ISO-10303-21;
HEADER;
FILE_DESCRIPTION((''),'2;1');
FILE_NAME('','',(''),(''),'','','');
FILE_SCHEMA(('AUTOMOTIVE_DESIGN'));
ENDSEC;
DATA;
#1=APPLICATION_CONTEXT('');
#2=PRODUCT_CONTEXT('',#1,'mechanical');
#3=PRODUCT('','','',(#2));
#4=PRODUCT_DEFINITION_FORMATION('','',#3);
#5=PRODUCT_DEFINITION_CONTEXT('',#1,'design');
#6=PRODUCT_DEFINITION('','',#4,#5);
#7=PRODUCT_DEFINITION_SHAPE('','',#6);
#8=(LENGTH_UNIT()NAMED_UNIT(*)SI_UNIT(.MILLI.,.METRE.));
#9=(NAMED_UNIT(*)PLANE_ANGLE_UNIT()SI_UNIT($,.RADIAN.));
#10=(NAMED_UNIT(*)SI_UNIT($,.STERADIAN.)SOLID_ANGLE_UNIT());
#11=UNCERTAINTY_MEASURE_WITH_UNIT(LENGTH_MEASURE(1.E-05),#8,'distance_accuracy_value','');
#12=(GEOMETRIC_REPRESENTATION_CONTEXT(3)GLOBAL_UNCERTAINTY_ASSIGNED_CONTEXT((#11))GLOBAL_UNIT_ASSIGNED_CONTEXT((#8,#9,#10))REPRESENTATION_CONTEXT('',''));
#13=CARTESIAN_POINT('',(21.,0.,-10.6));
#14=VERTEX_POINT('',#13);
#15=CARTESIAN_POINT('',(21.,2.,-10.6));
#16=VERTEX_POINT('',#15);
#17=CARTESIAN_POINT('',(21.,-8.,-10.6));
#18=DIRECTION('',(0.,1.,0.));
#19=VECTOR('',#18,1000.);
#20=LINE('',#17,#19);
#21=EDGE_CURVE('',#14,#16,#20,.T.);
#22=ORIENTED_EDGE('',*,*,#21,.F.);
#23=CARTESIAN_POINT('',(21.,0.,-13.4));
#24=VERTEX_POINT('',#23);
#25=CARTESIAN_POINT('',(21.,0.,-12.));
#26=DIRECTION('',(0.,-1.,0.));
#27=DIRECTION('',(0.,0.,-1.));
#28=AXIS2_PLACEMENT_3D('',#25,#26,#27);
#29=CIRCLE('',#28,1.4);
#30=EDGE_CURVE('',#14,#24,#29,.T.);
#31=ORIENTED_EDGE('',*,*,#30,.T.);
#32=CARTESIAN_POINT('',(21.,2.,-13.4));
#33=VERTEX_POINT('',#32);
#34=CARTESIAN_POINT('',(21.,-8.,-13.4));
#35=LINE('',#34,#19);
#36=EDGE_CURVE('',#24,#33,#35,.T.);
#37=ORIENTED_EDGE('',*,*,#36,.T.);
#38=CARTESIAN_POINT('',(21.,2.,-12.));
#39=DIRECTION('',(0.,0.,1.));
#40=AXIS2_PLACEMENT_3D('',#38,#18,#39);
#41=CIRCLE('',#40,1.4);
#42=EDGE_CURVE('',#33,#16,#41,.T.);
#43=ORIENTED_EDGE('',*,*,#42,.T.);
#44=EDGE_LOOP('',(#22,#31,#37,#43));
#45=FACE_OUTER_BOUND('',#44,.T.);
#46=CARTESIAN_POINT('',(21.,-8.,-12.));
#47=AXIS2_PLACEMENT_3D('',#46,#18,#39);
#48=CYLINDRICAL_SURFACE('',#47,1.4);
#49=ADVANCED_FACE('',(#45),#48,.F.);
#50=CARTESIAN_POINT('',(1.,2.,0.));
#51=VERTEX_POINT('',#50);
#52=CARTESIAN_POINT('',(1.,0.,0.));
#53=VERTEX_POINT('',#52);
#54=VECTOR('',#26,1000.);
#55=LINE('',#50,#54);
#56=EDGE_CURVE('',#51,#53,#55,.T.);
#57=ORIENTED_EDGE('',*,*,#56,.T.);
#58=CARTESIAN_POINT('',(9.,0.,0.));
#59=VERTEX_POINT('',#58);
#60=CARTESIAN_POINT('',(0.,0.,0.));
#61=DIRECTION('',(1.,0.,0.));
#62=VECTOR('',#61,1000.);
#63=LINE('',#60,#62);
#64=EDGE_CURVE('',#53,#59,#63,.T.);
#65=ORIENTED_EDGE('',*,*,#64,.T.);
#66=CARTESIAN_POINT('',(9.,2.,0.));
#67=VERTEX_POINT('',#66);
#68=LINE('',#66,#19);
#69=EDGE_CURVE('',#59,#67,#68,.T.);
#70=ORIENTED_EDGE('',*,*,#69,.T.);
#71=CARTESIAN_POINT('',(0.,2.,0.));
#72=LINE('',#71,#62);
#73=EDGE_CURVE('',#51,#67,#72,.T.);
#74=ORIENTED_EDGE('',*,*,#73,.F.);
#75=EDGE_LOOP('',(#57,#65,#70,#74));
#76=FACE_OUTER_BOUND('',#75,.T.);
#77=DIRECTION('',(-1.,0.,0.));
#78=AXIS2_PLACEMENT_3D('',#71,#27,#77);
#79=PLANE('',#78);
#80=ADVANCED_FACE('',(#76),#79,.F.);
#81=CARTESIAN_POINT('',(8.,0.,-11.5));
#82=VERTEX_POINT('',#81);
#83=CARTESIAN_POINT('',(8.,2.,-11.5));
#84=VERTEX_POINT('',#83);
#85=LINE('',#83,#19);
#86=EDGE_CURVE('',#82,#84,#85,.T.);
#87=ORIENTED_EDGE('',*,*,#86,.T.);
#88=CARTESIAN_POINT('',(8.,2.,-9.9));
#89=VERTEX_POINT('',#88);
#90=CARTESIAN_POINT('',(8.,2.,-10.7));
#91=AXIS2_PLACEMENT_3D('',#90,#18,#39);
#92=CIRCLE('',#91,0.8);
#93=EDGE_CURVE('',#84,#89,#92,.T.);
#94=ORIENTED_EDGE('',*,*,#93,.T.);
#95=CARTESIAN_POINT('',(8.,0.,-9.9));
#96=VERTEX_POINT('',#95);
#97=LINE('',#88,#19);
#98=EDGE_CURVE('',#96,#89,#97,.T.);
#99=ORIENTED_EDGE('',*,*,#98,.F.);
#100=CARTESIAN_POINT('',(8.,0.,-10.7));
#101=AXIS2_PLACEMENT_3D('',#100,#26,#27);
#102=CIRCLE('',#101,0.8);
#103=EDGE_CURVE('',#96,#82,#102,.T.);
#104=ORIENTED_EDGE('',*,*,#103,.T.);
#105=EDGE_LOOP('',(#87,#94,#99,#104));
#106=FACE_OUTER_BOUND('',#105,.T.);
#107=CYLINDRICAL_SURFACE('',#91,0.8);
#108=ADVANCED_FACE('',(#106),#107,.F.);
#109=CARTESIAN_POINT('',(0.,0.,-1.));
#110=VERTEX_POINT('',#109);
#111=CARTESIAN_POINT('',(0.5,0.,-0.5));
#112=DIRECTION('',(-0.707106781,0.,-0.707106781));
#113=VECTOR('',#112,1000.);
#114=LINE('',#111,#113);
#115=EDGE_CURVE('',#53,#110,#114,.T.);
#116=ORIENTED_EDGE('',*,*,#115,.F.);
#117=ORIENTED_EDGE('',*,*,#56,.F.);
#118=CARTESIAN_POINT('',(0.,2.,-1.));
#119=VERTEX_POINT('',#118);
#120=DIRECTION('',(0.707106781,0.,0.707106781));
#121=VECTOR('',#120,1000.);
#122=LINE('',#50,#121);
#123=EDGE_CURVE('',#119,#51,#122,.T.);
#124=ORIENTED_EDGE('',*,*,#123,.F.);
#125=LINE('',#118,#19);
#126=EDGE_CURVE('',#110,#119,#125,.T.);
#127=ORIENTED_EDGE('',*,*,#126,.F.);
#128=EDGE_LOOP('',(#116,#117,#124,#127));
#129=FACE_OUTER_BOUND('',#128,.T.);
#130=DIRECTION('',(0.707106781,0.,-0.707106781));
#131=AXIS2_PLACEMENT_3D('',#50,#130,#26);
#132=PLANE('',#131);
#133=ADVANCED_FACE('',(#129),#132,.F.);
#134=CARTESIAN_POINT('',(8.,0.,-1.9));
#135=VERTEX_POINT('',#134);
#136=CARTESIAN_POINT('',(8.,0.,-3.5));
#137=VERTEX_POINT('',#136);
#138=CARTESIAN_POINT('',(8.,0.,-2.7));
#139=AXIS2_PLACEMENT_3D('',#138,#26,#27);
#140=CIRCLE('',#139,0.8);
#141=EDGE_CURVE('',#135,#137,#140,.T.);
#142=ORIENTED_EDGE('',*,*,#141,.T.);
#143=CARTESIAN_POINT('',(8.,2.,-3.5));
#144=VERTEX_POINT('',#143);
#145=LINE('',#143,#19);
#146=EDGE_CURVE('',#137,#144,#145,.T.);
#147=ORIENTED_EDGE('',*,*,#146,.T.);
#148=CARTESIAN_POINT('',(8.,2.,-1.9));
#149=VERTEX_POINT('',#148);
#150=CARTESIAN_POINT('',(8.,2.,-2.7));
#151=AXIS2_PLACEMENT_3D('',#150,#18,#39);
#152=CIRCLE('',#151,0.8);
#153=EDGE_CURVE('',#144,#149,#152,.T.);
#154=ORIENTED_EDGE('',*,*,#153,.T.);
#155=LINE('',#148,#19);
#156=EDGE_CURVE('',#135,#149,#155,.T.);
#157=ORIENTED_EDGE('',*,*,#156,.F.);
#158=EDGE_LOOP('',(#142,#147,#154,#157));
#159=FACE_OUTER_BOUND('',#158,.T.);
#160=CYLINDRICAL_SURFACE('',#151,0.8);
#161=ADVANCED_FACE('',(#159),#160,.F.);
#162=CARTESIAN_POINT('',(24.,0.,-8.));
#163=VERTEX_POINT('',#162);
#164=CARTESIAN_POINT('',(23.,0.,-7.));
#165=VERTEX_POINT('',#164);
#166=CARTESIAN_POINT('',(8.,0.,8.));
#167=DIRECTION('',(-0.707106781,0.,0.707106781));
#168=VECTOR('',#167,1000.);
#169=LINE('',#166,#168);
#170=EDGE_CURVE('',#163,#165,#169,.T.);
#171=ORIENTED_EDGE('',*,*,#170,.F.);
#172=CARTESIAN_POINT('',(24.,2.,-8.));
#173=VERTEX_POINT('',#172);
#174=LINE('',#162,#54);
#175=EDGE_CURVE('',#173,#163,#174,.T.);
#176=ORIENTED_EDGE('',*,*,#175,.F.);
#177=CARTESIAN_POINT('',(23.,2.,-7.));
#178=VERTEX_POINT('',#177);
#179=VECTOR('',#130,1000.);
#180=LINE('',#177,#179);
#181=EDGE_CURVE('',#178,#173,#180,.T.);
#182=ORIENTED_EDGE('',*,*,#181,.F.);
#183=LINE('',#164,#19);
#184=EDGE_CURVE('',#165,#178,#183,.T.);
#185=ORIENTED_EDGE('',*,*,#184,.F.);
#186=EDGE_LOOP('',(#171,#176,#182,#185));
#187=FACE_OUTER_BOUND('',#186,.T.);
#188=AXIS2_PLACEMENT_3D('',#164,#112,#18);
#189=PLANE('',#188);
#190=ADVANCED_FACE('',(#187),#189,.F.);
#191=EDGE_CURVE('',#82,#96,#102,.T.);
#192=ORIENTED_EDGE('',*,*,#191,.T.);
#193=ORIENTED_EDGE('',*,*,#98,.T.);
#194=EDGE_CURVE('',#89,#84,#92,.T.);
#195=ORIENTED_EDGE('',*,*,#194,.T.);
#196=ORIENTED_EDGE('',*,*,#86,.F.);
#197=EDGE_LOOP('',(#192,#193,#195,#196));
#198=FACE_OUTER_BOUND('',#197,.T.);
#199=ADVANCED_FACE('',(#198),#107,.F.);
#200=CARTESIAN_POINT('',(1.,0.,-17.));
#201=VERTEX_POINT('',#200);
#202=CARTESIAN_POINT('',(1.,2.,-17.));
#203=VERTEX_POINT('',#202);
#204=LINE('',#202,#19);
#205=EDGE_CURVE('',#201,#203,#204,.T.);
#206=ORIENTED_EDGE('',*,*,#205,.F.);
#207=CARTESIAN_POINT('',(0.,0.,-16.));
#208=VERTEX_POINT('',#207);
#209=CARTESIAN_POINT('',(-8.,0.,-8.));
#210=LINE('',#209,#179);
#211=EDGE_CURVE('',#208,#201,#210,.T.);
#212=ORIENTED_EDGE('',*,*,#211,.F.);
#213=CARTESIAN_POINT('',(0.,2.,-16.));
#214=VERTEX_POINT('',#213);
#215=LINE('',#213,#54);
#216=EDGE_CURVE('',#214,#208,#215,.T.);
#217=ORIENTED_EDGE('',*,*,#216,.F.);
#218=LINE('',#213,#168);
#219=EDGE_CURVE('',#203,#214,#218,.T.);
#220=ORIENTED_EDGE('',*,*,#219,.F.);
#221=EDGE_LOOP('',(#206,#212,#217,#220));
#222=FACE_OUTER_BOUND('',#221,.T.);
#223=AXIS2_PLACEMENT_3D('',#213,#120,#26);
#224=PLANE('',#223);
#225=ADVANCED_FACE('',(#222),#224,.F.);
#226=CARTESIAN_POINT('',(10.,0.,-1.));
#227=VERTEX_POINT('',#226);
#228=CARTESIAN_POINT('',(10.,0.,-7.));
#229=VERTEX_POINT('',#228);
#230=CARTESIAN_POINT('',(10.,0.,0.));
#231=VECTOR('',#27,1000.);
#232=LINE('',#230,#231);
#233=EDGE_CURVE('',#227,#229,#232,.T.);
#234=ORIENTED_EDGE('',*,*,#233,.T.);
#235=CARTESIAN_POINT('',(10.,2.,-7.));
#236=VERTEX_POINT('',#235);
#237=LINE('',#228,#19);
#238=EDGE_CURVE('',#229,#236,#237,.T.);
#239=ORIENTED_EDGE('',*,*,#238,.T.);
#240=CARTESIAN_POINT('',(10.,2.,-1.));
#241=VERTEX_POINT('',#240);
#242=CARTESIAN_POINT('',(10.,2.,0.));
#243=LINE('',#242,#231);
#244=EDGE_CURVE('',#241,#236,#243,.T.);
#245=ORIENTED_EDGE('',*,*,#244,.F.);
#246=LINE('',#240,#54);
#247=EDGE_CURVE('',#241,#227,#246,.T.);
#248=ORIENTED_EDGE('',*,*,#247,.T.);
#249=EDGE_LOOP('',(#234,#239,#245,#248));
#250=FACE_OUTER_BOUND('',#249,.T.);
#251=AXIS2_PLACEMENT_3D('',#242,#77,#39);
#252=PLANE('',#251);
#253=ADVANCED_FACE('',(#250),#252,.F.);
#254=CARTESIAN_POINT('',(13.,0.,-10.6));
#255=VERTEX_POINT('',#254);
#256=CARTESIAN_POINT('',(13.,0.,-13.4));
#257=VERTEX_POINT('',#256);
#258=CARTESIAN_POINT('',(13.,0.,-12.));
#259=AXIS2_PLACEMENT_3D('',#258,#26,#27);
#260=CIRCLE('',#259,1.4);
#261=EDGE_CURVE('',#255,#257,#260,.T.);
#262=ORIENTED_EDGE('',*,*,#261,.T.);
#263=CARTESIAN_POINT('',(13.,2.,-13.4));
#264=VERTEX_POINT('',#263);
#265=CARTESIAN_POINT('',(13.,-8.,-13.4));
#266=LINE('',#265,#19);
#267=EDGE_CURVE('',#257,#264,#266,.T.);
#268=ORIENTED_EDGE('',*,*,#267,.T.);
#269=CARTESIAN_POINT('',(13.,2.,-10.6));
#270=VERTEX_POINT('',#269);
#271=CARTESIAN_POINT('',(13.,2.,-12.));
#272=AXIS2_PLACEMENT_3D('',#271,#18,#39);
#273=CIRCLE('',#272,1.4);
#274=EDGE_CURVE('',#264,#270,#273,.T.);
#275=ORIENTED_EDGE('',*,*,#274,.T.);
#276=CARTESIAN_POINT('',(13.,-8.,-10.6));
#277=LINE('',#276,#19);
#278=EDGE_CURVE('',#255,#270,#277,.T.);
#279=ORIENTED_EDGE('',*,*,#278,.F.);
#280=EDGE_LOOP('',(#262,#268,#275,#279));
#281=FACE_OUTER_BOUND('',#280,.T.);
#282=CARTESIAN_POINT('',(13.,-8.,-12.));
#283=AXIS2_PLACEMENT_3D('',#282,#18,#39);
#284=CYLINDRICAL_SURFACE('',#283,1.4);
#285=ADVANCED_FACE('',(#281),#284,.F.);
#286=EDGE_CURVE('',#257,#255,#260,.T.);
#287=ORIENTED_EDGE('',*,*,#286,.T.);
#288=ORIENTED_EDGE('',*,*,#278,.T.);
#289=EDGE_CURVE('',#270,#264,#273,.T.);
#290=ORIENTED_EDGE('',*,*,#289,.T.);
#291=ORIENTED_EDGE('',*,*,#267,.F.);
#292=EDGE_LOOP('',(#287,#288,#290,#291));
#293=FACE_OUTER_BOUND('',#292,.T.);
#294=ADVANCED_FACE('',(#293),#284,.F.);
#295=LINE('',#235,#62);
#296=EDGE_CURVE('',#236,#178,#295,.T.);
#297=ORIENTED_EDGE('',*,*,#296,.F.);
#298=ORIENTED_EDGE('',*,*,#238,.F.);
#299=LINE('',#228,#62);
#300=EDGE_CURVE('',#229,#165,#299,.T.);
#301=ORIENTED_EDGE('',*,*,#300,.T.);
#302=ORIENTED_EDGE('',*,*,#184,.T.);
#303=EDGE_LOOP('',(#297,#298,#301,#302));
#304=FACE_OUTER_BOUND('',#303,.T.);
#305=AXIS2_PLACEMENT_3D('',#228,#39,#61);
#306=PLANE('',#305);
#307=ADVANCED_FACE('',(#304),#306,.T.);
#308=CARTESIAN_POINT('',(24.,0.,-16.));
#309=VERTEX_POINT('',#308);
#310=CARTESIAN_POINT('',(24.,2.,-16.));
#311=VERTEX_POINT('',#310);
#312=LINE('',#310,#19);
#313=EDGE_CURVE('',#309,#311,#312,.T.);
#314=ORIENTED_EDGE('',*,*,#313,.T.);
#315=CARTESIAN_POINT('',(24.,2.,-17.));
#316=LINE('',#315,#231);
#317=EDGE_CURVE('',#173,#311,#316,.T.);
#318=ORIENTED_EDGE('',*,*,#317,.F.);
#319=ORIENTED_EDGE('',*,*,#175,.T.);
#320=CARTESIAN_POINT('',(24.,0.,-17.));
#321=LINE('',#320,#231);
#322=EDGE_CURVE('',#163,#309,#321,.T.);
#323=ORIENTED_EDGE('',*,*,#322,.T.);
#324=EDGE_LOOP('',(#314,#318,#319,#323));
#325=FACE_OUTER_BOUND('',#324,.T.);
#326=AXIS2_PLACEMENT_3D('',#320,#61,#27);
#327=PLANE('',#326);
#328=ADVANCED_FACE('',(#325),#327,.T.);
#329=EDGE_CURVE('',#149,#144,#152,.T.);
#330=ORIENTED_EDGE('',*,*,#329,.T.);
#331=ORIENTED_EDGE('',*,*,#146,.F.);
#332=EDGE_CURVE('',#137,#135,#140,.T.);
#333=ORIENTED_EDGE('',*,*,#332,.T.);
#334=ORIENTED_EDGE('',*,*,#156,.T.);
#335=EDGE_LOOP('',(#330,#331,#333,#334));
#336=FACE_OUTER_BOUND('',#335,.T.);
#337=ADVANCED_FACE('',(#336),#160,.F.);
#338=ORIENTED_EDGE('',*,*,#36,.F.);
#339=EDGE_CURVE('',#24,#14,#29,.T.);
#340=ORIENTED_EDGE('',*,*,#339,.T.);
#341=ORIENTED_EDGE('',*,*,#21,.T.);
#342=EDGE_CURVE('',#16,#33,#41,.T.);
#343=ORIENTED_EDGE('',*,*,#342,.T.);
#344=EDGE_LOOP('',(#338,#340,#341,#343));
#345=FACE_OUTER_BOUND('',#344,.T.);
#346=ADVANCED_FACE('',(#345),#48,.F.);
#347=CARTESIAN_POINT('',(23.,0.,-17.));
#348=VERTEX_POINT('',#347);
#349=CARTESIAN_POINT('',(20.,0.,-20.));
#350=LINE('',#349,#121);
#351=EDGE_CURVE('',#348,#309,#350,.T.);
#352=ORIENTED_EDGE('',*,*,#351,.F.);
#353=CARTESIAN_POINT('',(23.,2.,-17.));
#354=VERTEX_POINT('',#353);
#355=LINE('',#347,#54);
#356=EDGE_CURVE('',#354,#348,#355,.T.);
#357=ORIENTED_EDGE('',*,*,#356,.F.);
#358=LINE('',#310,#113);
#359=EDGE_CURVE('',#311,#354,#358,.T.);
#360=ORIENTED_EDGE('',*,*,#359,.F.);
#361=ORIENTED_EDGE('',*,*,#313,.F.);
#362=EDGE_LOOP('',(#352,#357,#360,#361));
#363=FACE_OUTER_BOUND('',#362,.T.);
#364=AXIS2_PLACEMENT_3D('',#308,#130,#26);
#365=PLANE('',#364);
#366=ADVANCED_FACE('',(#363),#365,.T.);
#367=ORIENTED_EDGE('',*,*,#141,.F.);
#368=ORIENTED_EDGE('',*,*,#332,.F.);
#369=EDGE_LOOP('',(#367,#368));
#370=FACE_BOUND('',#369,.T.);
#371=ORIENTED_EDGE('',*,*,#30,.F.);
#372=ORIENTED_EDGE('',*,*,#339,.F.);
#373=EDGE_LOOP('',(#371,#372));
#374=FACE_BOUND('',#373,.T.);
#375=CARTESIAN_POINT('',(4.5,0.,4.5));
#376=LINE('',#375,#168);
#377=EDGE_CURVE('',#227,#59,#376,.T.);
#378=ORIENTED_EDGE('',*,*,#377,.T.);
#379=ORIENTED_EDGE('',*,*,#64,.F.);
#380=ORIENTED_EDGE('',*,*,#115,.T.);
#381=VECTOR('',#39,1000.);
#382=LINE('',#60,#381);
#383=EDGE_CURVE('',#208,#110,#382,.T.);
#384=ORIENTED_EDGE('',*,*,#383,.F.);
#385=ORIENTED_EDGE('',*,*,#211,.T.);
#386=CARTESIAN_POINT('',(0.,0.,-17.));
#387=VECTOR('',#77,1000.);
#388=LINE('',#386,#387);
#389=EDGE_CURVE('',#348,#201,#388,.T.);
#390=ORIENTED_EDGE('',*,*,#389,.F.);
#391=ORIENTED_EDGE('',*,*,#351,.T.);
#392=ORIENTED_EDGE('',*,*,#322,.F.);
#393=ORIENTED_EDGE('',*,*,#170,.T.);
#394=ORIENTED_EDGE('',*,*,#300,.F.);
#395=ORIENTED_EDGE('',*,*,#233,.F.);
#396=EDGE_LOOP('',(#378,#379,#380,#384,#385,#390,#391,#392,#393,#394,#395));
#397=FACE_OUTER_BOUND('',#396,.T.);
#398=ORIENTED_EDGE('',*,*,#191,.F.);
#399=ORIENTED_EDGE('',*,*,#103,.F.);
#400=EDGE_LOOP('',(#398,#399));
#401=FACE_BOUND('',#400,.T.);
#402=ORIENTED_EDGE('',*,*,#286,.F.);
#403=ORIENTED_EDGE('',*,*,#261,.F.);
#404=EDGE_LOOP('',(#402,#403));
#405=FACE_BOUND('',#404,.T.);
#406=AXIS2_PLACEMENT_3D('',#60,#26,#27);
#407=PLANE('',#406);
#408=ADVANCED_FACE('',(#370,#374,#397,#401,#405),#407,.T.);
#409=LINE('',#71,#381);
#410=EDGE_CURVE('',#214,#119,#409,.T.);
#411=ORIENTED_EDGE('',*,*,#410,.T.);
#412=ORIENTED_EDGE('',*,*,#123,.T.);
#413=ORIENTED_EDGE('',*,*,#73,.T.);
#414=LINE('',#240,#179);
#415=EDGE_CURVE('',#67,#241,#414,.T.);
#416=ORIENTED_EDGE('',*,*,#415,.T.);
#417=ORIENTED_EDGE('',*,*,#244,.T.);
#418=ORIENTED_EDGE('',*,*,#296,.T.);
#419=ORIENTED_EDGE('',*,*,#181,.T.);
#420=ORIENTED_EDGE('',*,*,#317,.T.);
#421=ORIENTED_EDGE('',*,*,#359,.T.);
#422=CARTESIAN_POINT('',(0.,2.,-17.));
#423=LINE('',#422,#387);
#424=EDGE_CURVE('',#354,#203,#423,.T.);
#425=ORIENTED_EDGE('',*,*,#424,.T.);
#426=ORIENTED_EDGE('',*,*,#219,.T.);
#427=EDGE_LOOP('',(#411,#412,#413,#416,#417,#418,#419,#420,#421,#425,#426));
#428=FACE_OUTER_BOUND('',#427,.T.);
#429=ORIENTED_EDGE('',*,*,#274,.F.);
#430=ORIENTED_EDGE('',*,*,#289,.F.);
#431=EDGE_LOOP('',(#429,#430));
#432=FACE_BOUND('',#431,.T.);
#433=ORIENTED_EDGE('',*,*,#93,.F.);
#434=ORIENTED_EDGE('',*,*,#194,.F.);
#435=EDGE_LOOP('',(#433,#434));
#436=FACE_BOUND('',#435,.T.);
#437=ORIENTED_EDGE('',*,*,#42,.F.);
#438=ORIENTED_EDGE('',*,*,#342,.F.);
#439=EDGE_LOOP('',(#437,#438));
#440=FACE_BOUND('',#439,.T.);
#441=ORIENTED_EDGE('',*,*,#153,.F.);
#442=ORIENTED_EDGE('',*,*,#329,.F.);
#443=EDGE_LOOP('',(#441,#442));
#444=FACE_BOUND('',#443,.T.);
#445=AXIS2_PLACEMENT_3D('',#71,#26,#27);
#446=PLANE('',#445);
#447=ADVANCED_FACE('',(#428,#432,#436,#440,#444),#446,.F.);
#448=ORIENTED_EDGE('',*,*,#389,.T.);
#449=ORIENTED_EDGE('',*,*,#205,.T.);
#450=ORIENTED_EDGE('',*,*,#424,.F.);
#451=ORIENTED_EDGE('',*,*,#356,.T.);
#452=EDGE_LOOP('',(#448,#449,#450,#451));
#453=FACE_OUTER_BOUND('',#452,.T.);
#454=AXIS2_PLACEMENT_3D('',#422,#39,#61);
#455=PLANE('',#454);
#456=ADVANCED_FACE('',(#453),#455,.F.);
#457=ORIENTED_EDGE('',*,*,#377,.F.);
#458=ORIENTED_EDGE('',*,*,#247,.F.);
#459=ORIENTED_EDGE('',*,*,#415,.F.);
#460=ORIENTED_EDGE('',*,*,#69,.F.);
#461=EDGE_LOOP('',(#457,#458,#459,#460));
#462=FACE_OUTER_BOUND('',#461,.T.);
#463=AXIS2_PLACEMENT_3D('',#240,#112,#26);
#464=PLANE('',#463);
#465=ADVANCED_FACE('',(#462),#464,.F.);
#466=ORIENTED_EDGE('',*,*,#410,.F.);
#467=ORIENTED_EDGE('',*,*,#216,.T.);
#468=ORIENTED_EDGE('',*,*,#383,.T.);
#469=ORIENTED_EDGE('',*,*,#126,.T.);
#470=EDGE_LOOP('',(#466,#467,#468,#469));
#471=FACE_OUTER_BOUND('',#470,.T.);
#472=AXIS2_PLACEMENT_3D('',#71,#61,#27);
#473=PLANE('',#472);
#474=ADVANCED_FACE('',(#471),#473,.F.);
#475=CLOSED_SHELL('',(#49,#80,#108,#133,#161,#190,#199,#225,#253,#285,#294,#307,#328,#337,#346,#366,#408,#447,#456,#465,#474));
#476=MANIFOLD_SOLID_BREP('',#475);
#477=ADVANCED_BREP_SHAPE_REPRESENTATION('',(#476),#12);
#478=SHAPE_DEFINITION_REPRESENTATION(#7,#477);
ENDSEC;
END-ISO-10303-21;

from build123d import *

# Parameters (mm, degrees)
SKETCH1_W             = 10
SKETCH1_H             = 17
BOSS_EXTRUDE1_DEPTH   = 2
SKETCH2_W             = 14
SKETCH2_H             = 10
BOSS_EXTRUDE2_DEPTH   = 2
SKETCH3_R             = 1.4
CUT_EXTRUDE1_DEPTH    = 10
CHAMFER1_SIZE         = 1
M2_TAPPED_HOLE1_D     = 1.6
M2_TAPPED_HOLE1_DEPTH = 5.2
M2_TAPPED_HOLE1_TIP   = 0.480688495


with BuildPart() as part:
    # Sketch1 → Boss-Extrude1 (new body)
    with BuildSketch(Plane(origin=(0, 0, 0), x_dir=(1, 0, 0), z_dir=(0, 1, 0))):
        with Locations((5, 8.5)):
            Rectangle(SKETCH1_W, SKETCH1_H)
    extrude(amount=BOSS_EXTRUDE1_DEPTH)

    # Sketch2 → Boss-Extrude2 (add)
    with BuildSketch(Plane(origin=(0, 2, 0), x_dir=(1, 0, 0), z_dir=(0, 1, 0))):
        with Locations((17, 12)):
            Rectangle(SKETCH2_W, SKETCH2_H)
    extrude(amount=-BOSS_EXTRUDE2_DEPTH)

    # Sketch3 → Cut-Extrude1 (cut)
    with BuildSketch(Plane(origin=(0, 2, 0), x_dir=(1, 0, 0), z_dir=(0, 1, 0))):
        with Locations(Location((21, 12, 0), (0, 0, 270))):
            Circle(SKETCH3_R)
        with Locations(Location((13, 12, 0), (0, 0, 270))):
            Circle(SKETCH3_R)
    extrude(amount=-CUT_EXTRUDE1_DEPTH, mode=Mode.SUBTRACT)

    # Chamfer1
    chamfer1_edges = [part.edges().sort_by_distance(p)[0] for p in [
        (0, 1, -17),
        (0, 1, 0),
        (10, 1, 0),
        (24, 1, -17),
        (24, 1, -7),
    ]]
    chamfer(chamfer1_edges, length=CHAMFER1_SIZE)

    # M2 Tapped Hole1
    with Locations(Plane(origin=(0, 2, 0), x_dir=(1, 0, 0), z_dir=(0, 1, 0))):
        with Locations((8, 10.7), (8, 2.7)):
            Hole(M2_TAPPED_HOLE1_D / 2, depth=M2_TAPPED_HOLE1_DEPTH)
            with Locations((0, 0, -(M2_TAPPED_HOLE1_DEPTH + M2_TAPPED_HOLE1_TIP / 2))):  # 118° drill point
                Cone(0, M2_TAPPED_HOLE1_D / 2, M2_TAPPED_HOLE1_TIP, mode=Mode.SUBTRACT)


solid = part.part
